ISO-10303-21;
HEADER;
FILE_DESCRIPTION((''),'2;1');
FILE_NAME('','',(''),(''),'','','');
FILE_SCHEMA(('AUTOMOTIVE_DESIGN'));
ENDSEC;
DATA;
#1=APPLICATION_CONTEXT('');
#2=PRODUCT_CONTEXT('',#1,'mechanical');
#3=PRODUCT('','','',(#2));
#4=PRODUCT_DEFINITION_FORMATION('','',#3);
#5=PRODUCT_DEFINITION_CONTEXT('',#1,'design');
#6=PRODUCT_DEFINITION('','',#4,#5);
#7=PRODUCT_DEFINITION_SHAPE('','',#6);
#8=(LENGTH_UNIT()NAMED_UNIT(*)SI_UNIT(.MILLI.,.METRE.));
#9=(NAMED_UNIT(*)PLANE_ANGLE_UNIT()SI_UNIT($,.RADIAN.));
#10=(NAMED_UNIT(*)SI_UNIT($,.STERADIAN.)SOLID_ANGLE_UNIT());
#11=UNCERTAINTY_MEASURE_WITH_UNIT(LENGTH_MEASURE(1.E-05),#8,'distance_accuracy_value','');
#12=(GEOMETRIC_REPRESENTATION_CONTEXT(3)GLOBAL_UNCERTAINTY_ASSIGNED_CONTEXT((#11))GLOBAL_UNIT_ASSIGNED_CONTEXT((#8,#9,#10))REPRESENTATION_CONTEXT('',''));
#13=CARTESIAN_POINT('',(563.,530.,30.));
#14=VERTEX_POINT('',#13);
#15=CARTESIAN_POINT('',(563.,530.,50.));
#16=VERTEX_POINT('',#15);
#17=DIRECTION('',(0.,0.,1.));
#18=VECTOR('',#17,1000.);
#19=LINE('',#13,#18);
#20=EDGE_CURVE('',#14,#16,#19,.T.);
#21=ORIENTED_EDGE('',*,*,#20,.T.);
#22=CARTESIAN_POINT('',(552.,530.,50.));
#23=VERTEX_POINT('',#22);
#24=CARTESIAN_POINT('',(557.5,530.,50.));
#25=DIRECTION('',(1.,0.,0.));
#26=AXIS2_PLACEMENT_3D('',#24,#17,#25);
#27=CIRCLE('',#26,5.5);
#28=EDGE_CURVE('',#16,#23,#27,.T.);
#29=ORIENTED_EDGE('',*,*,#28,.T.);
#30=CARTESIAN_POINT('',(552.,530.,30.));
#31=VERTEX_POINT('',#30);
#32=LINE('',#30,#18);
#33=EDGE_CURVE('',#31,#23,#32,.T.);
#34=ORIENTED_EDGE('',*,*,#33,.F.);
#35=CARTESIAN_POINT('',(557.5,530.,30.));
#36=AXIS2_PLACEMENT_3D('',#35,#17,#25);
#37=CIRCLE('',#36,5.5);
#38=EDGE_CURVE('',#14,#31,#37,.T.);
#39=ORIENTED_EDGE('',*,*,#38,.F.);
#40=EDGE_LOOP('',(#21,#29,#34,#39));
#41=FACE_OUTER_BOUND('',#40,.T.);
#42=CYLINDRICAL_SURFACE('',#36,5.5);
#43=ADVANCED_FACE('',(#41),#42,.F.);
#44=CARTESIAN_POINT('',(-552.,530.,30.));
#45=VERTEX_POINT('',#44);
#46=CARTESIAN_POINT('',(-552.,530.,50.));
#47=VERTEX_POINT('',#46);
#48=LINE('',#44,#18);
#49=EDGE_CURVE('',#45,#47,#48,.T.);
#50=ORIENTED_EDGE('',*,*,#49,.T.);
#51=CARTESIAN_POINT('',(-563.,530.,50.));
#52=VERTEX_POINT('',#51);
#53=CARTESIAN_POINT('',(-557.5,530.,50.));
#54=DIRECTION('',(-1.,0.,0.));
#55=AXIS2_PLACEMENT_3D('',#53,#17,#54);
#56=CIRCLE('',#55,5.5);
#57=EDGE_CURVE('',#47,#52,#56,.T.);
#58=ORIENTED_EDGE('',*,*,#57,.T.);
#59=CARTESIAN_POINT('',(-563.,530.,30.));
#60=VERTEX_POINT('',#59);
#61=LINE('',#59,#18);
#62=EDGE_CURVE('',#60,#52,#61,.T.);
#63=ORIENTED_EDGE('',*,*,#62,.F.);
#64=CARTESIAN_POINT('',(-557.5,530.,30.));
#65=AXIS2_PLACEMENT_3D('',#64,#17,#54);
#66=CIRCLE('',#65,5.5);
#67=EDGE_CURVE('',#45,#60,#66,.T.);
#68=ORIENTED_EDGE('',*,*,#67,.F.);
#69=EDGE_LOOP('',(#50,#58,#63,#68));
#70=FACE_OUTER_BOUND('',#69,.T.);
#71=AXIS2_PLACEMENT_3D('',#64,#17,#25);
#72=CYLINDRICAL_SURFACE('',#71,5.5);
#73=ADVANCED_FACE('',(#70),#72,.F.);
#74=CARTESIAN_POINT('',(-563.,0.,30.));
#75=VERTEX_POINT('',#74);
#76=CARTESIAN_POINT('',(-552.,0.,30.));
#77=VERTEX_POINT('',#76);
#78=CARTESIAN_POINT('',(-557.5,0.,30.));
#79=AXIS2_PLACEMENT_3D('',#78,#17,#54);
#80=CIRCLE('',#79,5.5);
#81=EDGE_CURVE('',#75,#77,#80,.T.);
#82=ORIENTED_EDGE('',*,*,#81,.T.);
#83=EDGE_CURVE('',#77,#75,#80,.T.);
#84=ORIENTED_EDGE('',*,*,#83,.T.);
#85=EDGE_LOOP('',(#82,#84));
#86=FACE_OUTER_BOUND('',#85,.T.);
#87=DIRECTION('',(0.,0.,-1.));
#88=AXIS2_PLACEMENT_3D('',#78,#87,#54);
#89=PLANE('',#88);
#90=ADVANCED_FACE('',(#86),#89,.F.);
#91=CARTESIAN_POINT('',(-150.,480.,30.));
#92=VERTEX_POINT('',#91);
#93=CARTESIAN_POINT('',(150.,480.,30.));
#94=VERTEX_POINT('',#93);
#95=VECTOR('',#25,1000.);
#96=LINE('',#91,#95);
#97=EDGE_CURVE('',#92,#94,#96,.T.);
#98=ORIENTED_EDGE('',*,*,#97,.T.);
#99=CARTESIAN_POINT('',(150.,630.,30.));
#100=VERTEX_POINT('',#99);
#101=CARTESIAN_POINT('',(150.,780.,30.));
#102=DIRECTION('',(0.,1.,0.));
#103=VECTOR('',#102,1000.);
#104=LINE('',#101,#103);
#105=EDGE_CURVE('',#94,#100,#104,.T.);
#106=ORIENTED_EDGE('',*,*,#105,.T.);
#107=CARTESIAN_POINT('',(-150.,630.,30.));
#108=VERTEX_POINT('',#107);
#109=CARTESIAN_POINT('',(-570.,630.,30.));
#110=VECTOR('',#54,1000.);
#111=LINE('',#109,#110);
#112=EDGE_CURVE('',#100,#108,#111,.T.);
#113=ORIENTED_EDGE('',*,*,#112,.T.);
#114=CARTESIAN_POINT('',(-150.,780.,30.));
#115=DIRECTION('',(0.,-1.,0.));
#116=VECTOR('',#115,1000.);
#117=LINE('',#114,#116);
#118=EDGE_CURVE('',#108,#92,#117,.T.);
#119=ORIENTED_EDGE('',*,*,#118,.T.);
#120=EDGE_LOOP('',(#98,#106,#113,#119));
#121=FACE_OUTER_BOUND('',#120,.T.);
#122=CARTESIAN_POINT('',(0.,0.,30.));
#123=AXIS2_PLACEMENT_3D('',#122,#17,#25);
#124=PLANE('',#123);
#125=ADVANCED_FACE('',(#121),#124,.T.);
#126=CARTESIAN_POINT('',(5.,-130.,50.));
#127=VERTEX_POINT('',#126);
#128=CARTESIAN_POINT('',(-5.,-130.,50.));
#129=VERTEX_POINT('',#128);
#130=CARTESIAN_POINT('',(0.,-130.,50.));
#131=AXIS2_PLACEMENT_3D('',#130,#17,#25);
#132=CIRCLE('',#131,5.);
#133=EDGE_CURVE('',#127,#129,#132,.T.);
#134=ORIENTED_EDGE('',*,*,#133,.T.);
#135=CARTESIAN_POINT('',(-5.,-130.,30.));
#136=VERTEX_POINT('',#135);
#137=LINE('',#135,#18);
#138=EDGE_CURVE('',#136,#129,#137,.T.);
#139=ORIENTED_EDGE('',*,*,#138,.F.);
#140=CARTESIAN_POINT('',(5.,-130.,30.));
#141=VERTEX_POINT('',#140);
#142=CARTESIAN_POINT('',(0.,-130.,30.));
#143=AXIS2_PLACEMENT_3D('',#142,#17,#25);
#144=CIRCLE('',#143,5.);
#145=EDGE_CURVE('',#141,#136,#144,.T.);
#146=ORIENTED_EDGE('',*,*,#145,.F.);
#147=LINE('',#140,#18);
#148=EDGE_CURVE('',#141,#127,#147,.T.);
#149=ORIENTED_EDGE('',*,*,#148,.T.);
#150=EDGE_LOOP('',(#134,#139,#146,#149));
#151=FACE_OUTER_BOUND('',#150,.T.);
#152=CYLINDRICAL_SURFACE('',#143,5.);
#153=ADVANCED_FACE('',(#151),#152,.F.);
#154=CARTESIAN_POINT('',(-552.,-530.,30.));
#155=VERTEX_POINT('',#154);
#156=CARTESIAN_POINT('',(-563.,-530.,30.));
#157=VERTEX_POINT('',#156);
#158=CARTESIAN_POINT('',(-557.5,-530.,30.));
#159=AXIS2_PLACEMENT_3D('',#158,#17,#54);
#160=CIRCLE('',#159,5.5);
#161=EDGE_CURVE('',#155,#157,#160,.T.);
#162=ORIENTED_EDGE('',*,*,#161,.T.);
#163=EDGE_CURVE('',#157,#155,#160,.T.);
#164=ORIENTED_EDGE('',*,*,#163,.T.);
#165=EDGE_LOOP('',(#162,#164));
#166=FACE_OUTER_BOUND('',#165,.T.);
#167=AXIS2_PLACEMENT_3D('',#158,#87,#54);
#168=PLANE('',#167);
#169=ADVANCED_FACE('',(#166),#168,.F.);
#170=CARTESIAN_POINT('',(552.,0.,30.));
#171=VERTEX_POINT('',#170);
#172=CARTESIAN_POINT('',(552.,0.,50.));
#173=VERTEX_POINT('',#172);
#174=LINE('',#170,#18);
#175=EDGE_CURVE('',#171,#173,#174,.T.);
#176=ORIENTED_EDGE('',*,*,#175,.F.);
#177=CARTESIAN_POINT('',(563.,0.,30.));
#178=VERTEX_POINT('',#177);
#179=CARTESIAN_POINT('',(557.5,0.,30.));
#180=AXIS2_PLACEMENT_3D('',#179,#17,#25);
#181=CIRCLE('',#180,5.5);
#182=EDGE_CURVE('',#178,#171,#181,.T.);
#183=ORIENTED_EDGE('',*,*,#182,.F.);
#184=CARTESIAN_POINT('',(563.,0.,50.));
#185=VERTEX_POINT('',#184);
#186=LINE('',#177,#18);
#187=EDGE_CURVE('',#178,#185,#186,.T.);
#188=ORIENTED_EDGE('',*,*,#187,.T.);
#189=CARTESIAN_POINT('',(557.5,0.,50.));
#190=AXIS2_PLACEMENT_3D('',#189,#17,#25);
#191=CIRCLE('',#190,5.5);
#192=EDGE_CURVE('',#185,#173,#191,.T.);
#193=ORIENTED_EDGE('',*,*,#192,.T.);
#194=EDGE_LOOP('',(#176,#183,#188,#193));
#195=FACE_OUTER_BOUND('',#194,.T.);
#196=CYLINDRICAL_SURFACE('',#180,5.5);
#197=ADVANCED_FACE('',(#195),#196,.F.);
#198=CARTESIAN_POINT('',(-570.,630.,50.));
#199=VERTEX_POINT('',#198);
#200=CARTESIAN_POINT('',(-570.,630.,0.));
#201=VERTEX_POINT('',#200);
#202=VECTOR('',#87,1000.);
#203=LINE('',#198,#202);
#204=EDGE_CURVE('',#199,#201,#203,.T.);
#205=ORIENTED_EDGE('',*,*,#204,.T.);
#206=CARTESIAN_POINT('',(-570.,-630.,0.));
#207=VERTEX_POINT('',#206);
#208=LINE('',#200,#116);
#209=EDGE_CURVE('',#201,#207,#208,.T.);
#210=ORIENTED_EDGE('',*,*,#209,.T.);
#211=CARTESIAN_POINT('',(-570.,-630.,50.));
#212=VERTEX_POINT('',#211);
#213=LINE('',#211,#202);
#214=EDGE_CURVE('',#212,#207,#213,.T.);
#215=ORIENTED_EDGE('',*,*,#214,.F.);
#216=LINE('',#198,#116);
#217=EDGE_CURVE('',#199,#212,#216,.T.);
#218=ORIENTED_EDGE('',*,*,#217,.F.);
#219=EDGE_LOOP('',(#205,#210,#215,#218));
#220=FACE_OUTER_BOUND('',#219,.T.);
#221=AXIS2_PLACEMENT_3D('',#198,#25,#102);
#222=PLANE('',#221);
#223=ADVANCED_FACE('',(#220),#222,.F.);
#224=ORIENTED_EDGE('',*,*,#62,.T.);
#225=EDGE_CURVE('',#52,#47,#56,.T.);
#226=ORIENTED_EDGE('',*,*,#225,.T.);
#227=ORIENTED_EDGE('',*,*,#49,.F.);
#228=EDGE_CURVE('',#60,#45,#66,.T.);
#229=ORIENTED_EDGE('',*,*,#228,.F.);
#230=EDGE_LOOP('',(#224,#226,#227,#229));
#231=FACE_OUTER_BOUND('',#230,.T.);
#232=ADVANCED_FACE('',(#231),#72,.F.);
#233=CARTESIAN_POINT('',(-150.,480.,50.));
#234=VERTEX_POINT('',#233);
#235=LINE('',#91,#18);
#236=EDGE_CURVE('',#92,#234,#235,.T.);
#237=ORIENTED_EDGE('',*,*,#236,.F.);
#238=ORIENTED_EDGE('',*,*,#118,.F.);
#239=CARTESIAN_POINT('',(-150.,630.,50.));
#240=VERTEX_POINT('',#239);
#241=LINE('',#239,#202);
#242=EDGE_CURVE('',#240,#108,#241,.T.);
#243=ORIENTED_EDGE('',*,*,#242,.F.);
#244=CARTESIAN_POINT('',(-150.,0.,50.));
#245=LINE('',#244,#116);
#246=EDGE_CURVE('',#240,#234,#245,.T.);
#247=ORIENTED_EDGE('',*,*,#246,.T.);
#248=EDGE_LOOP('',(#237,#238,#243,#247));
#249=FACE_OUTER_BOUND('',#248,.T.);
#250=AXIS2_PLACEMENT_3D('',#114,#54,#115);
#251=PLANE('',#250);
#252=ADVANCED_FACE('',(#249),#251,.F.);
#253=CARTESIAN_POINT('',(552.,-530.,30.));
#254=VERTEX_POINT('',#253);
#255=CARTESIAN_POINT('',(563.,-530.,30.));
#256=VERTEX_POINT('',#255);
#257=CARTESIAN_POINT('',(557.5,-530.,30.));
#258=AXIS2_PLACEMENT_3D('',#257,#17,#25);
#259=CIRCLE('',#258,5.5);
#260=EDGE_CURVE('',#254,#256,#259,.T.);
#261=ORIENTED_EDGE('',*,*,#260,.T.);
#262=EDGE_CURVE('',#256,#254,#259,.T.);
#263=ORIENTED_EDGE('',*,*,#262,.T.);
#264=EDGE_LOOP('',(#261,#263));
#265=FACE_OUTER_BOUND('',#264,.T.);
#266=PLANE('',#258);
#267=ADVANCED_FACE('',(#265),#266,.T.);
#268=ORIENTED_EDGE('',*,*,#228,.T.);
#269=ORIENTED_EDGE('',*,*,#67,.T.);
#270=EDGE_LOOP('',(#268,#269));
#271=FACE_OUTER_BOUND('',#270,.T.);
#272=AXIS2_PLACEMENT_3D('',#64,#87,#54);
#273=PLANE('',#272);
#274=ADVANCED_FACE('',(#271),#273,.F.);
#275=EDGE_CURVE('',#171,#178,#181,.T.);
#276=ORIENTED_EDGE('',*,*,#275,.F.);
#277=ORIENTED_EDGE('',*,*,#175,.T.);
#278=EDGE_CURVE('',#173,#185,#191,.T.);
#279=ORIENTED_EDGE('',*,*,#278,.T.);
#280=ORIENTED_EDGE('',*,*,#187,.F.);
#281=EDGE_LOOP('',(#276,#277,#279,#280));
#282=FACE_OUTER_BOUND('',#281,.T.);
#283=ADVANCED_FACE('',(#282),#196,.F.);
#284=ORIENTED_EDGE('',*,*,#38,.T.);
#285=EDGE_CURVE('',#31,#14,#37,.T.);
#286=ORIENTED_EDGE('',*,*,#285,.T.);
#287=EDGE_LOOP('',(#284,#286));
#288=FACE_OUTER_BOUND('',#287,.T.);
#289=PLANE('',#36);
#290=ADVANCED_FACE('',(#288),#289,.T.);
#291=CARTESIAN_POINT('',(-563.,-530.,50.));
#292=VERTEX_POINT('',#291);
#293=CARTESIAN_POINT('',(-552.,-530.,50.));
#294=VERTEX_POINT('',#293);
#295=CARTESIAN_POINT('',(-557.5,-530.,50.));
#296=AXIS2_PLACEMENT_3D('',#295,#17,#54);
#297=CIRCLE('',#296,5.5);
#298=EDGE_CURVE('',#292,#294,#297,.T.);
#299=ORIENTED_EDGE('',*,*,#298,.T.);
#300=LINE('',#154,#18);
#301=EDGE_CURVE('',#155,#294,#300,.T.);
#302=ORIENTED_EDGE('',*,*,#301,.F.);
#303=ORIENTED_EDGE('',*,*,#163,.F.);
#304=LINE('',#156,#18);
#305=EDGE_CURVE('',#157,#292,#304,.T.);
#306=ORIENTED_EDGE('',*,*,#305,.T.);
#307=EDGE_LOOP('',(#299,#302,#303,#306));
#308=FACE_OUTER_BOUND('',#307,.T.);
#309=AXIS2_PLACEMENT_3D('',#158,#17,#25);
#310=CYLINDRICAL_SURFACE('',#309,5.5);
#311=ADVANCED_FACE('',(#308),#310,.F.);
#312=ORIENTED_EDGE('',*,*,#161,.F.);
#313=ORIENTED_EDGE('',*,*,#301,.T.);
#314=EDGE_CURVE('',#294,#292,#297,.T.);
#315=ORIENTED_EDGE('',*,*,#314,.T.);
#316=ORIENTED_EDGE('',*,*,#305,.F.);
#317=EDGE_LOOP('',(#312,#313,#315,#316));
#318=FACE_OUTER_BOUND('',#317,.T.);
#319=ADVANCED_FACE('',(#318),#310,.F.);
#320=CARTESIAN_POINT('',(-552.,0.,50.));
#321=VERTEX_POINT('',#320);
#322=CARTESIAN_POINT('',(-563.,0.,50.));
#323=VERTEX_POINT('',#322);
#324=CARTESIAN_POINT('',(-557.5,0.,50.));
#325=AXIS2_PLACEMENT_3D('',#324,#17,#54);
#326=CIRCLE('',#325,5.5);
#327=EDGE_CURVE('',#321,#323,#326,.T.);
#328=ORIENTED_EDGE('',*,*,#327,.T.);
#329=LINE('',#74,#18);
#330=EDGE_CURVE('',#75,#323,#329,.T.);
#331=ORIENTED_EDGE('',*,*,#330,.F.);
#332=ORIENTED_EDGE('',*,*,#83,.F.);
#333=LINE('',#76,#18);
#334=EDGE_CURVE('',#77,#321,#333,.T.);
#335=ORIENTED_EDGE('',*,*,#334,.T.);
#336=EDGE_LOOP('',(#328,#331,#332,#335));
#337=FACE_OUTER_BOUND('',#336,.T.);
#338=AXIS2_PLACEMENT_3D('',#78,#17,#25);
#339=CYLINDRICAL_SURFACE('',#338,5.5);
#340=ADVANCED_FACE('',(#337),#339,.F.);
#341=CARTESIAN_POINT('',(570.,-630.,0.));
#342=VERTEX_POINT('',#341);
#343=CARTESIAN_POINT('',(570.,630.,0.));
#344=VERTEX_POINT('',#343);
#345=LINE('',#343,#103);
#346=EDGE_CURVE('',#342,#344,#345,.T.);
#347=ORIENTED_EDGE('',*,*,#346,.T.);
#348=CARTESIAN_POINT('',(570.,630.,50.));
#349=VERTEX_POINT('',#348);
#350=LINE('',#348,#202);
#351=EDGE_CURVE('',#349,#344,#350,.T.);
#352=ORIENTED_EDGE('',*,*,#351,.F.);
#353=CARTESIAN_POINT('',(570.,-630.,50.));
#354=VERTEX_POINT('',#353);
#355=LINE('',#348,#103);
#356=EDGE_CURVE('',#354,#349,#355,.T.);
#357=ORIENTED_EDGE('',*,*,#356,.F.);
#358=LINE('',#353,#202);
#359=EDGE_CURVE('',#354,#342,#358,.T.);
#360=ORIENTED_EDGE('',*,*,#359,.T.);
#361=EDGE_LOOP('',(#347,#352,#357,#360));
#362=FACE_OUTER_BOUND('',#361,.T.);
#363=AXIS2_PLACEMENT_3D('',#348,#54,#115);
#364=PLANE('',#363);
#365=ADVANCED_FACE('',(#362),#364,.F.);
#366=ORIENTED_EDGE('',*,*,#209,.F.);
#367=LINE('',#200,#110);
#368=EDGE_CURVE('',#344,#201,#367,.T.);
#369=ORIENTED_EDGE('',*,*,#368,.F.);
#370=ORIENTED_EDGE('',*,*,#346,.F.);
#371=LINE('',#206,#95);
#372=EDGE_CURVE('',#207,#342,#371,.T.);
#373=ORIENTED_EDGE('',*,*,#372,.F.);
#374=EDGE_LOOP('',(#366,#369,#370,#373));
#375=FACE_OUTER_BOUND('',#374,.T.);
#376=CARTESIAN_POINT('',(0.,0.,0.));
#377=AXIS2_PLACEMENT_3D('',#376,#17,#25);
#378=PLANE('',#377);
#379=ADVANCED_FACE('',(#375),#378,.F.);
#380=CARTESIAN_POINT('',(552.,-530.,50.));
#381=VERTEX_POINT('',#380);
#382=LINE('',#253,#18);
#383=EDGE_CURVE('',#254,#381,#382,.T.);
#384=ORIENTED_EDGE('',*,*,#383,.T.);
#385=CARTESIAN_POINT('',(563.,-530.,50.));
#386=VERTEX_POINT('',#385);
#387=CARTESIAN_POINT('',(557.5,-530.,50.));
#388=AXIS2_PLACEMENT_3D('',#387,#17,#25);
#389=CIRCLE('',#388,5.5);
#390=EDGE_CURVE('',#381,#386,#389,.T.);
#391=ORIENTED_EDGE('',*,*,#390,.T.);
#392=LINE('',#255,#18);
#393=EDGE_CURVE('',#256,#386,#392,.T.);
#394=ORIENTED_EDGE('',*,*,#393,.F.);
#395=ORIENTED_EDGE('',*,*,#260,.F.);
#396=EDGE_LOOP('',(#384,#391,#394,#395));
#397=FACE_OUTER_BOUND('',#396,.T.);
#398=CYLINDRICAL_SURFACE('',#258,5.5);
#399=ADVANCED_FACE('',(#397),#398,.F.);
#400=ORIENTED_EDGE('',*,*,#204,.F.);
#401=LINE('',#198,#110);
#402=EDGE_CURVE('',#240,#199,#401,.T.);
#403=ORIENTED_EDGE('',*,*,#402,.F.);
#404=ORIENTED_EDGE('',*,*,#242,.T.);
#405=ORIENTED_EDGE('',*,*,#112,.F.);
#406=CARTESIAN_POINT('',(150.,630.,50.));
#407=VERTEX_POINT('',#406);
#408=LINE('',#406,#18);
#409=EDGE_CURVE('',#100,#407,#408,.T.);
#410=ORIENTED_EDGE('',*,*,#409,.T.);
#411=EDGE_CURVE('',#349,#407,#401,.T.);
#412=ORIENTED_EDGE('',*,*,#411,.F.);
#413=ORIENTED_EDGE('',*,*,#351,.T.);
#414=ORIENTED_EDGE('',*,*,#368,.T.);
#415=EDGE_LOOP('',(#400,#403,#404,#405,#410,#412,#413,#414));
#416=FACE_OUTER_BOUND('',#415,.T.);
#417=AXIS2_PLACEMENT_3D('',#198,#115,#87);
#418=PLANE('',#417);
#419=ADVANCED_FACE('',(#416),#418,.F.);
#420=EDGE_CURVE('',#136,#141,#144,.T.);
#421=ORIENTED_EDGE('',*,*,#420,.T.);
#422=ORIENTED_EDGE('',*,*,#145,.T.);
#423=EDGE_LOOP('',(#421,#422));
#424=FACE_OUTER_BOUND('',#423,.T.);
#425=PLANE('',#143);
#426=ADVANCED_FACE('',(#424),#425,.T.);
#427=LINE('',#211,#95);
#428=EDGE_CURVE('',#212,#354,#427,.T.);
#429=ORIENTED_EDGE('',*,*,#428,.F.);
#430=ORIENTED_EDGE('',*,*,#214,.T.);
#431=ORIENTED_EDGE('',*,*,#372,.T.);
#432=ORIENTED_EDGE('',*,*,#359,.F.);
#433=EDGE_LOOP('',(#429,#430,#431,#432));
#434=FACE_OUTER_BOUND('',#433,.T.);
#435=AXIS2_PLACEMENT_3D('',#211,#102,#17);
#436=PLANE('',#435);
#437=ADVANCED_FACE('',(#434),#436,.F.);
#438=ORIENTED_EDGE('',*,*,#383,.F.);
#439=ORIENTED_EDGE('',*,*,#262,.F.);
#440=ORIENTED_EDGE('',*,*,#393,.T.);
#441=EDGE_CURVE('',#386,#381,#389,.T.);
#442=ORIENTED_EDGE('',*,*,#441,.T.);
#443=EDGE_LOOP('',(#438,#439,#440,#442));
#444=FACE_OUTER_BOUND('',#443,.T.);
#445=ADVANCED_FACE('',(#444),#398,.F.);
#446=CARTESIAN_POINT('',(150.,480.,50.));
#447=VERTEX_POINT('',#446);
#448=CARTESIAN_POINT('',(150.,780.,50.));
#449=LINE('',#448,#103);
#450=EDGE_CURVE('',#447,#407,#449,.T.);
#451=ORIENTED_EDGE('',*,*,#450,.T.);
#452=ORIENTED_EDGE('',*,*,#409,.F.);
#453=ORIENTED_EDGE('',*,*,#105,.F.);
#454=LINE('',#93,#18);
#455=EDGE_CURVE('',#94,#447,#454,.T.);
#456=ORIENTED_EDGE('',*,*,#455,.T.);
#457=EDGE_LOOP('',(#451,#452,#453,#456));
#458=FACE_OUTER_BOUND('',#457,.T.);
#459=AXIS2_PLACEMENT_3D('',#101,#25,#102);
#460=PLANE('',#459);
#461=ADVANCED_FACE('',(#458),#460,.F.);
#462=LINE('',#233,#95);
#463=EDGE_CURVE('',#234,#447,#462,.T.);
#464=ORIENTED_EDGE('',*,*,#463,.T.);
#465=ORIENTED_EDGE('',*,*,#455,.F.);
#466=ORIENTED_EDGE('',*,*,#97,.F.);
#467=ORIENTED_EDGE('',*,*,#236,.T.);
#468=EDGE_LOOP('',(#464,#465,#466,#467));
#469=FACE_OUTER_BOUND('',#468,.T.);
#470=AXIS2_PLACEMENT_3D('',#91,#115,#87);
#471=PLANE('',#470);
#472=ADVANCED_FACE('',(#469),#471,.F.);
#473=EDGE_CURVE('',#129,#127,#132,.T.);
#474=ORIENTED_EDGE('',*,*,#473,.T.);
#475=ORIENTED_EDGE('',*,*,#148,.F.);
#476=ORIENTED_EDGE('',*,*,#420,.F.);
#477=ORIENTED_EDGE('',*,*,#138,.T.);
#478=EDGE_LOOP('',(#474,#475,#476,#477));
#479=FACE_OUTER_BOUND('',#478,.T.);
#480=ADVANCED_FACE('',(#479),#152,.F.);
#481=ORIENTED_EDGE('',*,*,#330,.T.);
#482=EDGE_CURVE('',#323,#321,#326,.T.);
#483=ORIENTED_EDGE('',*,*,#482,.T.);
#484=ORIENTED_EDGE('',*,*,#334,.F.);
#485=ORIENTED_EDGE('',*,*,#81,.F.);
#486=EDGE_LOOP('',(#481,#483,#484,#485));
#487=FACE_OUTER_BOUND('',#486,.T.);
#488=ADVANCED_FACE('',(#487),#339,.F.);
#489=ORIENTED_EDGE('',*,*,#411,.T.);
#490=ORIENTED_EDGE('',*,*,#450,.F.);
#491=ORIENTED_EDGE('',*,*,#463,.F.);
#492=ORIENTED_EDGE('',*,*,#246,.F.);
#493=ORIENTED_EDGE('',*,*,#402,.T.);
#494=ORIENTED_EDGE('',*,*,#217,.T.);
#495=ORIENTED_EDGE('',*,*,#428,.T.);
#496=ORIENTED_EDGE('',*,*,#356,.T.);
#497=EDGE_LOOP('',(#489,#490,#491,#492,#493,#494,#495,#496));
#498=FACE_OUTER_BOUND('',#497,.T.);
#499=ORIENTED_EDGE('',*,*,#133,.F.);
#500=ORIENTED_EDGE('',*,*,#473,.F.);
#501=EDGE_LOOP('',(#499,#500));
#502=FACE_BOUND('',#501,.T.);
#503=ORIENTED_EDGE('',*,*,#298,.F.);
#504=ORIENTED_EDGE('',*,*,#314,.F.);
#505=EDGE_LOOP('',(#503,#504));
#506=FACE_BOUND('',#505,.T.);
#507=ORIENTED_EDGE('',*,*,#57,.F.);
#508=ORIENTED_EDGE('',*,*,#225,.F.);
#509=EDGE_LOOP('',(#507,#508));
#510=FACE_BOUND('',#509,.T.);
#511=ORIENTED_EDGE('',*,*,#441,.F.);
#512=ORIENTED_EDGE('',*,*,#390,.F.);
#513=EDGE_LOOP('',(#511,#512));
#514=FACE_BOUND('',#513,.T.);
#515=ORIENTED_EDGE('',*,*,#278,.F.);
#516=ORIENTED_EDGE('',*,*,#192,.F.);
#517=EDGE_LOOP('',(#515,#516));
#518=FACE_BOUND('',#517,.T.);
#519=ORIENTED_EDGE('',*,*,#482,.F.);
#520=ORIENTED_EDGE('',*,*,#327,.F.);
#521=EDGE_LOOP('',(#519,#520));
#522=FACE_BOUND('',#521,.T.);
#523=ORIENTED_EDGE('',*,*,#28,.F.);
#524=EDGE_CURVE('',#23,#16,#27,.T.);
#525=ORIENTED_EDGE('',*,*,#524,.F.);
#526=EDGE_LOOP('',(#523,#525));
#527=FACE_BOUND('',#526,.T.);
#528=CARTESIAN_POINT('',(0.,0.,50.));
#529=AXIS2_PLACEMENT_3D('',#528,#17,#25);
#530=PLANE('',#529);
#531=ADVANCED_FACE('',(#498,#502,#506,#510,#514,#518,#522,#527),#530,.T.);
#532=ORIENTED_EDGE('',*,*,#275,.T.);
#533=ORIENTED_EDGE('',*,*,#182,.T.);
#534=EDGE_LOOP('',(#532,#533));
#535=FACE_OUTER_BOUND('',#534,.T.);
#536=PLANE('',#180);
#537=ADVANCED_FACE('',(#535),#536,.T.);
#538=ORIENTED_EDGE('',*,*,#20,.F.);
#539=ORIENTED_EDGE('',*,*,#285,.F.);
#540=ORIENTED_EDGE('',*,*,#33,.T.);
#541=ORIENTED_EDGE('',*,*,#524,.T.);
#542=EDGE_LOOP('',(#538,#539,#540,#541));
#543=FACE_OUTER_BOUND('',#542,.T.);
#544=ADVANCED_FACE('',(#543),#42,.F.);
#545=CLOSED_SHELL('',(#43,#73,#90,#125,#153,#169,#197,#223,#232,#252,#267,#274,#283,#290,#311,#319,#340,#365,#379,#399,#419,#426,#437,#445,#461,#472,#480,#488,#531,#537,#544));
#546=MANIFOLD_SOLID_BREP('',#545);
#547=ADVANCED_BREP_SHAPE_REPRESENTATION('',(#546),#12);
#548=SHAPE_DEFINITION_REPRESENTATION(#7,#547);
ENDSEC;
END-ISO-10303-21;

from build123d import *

# Parameters (mm, degrees)
SKETCH_1_W            = 1140
SKETCH_1_H            = 1260
EXTRUDE_1_DEPTH       = 50
SKETCH_2_R            = 5
SKETCH_2_R_2          = 5.5
SKETCH_2_W            = 300
SKETCH_2_H            = 300
CUT_EXTRUDE_986_DEPTH = 20


with BuildPart() as part:
    # 草图1 → 凸台-拉伸1 (new body)
    with BuildSketch(Plane.XY):
        Rectangle(SKETCH_1_W, SKETCH_1_H)
    extrude(amount=EXTRUDE_1_DEPTH)

    # 草图2 → Cut-Extrude 986 (cut)
    with BuildSketch(Plane.XY.offset(50)):
        with Locations((0, -130)):
            Circle(SKETCH_2_R)
        with Locations((557.5, -530)):
            Circle(SKETCH_2_R_2)
        with Locations((557.5, 0)):
            Circle(SKETCH_2_R_2)
        with Locations((557.5, 530)):
            Circle(SKETCH_2_R_2)
        with Locations(Location((-557.5, 530, 0), (0, 0, 180))):
            Circle(SKETCH_2_R_2)
        with Locations(Location((-557.5, 0, 0), (0, 0, 180))):
            Circle(SKETCH_2_R_2)
        with Locations(Location((-557.5, -530, 0), (0, 0, 180))):
            Circle(SKETCH_2_R_2)
        with Locations((0, 630)):
            Rectangle(SKETCH_2_W, SKETCH_2_H)
    extrude(amount=-CUT_EXTRUDE_986_DEPTH, mode=Mode.SUBTRACT)


solid = part.part
